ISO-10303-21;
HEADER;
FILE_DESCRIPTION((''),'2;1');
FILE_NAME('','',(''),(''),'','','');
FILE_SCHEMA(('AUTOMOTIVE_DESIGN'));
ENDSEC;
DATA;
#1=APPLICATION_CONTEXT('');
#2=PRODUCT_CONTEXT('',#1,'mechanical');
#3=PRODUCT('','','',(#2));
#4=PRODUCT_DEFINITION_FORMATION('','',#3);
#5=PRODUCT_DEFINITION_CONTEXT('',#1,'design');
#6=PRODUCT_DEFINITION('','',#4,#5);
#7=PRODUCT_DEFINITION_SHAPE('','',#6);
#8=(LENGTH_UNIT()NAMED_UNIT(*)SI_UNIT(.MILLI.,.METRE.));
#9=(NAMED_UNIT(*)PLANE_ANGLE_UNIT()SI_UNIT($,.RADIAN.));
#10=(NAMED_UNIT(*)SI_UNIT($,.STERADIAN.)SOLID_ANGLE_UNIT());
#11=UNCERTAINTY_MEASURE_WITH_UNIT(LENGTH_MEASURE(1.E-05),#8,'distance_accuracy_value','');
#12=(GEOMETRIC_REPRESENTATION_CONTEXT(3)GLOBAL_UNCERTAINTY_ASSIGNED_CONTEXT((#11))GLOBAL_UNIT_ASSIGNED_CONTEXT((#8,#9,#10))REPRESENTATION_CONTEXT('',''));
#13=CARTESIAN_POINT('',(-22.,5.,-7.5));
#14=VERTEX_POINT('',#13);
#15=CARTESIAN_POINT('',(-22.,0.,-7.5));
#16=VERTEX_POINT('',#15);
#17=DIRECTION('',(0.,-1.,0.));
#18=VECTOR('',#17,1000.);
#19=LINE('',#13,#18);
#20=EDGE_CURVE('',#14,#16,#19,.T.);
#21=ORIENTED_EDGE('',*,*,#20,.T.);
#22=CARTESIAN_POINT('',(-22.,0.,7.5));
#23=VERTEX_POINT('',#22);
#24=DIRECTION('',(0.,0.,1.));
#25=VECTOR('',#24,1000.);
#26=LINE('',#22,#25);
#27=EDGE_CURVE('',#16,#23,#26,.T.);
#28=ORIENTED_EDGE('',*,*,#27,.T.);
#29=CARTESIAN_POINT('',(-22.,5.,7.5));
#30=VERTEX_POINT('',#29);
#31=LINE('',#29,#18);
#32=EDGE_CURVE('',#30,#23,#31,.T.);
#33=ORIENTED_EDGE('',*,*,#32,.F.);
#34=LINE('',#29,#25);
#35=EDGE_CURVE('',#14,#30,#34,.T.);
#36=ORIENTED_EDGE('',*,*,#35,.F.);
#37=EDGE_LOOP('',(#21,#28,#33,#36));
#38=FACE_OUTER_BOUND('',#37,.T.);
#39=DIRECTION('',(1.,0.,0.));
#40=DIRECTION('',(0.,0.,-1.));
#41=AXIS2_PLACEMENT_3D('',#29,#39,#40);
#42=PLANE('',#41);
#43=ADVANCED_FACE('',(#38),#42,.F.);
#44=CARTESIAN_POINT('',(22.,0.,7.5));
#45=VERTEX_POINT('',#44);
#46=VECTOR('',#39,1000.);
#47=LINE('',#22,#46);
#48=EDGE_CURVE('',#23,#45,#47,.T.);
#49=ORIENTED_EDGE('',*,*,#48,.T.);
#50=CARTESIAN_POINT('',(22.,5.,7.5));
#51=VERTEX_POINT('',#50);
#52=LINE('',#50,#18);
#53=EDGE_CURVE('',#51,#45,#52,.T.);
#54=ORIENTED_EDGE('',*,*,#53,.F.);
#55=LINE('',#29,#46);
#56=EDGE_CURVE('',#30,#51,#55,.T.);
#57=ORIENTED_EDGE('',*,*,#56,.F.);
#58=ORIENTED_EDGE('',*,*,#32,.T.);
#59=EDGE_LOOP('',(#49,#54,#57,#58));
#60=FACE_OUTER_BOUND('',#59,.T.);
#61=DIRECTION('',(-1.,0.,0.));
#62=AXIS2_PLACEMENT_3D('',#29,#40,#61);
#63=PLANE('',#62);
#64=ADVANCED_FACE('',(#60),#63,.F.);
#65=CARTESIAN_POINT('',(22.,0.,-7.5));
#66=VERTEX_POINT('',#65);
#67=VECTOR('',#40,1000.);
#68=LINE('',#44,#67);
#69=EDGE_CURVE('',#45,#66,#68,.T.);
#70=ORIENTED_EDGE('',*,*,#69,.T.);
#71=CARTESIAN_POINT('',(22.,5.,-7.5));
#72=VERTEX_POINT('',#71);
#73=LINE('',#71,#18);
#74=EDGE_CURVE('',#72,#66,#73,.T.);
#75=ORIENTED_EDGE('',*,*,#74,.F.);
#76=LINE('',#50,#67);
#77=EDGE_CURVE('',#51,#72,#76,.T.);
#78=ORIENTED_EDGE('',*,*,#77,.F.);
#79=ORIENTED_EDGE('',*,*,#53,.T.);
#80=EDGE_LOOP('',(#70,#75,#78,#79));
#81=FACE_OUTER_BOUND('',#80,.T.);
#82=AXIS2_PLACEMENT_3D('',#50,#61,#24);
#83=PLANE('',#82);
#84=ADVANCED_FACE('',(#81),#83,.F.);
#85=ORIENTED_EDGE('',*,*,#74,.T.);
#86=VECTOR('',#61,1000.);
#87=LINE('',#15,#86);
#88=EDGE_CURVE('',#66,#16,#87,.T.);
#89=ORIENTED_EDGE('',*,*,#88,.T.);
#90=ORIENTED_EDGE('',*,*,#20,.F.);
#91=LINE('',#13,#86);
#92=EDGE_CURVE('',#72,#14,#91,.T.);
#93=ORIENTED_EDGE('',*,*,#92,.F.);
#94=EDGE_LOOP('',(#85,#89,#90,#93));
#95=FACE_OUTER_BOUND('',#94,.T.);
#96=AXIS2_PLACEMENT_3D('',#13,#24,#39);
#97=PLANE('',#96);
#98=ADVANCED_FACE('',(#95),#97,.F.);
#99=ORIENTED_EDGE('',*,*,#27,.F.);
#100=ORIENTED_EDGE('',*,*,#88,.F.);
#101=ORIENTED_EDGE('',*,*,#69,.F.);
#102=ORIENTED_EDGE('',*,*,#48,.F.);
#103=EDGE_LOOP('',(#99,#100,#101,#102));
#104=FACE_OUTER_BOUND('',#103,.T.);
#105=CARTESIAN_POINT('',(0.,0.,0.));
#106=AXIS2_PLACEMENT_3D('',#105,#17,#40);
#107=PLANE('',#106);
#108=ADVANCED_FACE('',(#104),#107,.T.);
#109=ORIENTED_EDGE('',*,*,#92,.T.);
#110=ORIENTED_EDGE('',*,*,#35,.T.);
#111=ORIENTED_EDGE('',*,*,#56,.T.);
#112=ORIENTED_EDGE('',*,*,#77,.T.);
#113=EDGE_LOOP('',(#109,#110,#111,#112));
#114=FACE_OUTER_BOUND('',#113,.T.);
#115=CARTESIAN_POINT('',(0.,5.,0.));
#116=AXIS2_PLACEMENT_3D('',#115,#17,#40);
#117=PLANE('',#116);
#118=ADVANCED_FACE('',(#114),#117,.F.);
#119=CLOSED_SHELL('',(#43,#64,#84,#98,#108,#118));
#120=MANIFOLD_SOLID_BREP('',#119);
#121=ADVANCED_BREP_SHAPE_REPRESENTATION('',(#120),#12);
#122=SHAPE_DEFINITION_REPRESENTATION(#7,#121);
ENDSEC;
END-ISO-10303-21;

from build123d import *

# Parameters (mm, degrees)
SKETCH_1_W      = 44
SKETCH_1_H      = 15
EXTRUDE_1_DEPTH = 5


with BuildPart() as part:
    # 草图1 → 凸台-拉伸1 (new body)
    with BuildSketch(Plane(origin=(0, 0, 0), x_dir=(1, 0, 0), z_dir=(0, 1, 0))):
        Rectangle(SKETCH_1_W, SKETCH_1_H)
    extrude(amount=EXTRUDE_1_DEPTH)


solid = part.part
